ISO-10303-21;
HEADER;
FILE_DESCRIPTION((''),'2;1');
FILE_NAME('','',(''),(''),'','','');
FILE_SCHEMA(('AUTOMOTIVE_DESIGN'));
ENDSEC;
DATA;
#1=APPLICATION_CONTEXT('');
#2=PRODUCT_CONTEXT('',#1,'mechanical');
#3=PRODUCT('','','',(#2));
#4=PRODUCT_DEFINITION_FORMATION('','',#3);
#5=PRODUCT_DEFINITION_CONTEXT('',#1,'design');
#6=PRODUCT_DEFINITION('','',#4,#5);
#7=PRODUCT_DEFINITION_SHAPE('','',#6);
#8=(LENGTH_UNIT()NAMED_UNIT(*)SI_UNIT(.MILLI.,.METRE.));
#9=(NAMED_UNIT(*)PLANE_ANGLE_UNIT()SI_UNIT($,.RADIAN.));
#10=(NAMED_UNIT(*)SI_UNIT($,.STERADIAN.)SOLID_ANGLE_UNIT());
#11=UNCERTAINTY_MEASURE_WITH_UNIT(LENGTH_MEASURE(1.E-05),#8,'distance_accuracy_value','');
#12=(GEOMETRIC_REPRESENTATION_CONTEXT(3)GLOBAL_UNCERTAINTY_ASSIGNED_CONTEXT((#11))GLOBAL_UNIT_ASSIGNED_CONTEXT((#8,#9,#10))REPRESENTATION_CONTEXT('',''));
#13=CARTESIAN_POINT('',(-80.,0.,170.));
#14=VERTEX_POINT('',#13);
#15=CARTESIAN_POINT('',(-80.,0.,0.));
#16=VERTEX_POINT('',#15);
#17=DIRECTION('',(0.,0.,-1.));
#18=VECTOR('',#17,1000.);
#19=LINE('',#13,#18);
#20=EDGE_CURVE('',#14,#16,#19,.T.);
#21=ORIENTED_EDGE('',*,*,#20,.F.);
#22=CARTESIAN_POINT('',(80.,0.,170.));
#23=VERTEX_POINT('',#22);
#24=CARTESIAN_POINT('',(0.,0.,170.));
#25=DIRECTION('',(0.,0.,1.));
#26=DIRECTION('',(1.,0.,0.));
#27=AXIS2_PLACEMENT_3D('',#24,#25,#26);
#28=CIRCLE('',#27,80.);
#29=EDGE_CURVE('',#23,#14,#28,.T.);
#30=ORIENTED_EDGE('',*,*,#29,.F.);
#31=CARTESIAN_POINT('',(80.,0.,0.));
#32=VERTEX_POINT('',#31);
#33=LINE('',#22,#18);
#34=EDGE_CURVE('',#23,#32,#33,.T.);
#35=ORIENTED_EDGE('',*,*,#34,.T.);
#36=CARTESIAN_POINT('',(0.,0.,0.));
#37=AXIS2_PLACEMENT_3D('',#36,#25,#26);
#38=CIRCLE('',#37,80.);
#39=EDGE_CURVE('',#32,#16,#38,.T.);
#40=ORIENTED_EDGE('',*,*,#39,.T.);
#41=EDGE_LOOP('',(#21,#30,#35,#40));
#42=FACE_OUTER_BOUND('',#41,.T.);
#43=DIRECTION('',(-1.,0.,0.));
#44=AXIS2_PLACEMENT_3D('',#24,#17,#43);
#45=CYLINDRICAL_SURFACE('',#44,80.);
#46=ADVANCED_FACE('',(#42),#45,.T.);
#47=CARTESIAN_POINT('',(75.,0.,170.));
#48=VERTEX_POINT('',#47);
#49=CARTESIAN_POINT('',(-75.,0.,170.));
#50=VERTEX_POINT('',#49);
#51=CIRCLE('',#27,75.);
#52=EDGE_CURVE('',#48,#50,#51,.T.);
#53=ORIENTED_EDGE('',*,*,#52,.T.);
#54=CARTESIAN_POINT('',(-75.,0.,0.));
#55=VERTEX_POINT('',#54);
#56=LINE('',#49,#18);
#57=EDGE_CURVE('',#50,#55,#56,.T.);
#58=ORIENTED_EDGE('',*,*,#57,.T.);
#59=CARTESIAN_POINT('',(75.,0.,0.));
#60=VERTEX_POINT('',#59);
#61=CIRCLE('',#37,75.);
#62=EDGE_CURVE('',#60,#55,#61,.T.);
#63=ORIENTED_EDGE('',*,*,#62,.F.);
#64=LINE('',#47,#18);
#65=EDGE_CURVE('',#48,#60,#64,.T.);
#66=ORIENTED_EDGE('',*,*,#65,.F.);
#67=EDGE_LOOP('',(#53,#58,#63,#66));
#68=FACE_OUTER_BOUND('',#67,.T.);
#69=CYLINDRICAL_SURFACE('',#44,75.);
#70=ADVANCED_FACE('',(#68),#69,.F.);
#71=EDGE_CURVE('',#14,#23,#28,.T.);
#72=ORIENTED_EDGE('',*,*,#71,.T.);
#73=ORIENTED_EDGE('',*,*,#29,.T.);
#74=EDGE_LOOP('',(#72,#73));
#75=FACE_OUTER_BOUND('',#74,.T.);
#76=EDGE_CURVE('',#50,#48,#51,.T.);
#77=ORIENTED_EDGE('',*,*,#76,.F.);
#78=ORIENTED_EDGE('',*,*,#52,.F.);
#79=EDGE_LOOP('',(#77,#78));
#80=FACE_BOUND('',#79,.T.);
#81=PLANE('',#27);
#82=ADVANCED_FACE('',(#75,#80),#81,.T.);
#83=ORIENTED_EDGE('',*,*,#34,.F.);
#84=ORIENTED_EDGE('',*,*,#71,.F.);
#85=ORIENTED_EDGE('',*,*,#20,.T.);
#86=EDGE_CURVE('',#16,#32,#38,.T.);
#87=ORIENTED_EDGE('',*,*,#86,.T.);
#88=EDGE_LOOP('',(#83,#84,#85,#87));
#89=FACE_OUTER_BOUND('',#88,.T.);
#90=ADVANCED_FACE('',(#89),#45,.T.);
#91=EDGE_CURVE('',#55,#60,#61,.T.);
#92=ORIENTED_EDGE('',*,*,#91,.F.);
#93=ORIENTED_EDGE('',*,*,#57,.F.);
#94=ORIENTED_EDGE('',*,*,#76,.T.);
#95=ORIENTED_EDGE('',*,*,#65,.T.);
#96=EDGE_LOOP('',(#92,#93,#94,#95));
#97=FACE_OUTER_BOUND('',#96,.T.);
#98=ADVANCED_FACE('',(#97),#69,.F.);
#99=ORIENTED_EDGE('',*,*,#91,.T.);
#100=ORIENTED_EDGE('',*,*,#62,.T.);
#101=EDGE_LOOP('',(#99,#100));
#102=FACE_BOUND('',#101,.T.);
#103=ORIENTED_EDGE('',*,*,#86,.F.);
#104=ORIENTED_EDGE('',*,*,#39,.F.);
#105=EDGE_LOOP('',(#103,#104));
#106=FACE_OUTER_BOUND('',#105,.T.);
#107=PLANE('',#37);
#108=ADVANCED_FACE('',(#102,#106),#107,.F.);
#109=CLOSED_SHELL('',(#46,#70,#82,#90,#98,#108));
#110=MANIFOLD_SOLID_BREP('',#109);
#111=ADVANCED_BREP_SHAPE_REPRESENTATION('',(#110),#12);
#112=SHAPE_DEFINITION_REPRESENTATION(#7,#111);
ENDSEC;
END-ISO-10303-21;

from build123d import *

# Parameters (mm, degrees)
SKETCH_1_R      = 80
SKETCH_1_R_2    = 75
EXTRUDE_1_DEPTH = 170


with BuildPart() as part:
    # 草图1 → 凸台-拉伸1 (new body)
    with BuildSketch(Plane.XY):
        Circle(SKETCH_1_R)
        Circle(SKETCH_1_R_2, mode=Mode.SUBTRACT)
    extrude(amount=EXTRUDE_1_DEPTH)


solid = part.part
